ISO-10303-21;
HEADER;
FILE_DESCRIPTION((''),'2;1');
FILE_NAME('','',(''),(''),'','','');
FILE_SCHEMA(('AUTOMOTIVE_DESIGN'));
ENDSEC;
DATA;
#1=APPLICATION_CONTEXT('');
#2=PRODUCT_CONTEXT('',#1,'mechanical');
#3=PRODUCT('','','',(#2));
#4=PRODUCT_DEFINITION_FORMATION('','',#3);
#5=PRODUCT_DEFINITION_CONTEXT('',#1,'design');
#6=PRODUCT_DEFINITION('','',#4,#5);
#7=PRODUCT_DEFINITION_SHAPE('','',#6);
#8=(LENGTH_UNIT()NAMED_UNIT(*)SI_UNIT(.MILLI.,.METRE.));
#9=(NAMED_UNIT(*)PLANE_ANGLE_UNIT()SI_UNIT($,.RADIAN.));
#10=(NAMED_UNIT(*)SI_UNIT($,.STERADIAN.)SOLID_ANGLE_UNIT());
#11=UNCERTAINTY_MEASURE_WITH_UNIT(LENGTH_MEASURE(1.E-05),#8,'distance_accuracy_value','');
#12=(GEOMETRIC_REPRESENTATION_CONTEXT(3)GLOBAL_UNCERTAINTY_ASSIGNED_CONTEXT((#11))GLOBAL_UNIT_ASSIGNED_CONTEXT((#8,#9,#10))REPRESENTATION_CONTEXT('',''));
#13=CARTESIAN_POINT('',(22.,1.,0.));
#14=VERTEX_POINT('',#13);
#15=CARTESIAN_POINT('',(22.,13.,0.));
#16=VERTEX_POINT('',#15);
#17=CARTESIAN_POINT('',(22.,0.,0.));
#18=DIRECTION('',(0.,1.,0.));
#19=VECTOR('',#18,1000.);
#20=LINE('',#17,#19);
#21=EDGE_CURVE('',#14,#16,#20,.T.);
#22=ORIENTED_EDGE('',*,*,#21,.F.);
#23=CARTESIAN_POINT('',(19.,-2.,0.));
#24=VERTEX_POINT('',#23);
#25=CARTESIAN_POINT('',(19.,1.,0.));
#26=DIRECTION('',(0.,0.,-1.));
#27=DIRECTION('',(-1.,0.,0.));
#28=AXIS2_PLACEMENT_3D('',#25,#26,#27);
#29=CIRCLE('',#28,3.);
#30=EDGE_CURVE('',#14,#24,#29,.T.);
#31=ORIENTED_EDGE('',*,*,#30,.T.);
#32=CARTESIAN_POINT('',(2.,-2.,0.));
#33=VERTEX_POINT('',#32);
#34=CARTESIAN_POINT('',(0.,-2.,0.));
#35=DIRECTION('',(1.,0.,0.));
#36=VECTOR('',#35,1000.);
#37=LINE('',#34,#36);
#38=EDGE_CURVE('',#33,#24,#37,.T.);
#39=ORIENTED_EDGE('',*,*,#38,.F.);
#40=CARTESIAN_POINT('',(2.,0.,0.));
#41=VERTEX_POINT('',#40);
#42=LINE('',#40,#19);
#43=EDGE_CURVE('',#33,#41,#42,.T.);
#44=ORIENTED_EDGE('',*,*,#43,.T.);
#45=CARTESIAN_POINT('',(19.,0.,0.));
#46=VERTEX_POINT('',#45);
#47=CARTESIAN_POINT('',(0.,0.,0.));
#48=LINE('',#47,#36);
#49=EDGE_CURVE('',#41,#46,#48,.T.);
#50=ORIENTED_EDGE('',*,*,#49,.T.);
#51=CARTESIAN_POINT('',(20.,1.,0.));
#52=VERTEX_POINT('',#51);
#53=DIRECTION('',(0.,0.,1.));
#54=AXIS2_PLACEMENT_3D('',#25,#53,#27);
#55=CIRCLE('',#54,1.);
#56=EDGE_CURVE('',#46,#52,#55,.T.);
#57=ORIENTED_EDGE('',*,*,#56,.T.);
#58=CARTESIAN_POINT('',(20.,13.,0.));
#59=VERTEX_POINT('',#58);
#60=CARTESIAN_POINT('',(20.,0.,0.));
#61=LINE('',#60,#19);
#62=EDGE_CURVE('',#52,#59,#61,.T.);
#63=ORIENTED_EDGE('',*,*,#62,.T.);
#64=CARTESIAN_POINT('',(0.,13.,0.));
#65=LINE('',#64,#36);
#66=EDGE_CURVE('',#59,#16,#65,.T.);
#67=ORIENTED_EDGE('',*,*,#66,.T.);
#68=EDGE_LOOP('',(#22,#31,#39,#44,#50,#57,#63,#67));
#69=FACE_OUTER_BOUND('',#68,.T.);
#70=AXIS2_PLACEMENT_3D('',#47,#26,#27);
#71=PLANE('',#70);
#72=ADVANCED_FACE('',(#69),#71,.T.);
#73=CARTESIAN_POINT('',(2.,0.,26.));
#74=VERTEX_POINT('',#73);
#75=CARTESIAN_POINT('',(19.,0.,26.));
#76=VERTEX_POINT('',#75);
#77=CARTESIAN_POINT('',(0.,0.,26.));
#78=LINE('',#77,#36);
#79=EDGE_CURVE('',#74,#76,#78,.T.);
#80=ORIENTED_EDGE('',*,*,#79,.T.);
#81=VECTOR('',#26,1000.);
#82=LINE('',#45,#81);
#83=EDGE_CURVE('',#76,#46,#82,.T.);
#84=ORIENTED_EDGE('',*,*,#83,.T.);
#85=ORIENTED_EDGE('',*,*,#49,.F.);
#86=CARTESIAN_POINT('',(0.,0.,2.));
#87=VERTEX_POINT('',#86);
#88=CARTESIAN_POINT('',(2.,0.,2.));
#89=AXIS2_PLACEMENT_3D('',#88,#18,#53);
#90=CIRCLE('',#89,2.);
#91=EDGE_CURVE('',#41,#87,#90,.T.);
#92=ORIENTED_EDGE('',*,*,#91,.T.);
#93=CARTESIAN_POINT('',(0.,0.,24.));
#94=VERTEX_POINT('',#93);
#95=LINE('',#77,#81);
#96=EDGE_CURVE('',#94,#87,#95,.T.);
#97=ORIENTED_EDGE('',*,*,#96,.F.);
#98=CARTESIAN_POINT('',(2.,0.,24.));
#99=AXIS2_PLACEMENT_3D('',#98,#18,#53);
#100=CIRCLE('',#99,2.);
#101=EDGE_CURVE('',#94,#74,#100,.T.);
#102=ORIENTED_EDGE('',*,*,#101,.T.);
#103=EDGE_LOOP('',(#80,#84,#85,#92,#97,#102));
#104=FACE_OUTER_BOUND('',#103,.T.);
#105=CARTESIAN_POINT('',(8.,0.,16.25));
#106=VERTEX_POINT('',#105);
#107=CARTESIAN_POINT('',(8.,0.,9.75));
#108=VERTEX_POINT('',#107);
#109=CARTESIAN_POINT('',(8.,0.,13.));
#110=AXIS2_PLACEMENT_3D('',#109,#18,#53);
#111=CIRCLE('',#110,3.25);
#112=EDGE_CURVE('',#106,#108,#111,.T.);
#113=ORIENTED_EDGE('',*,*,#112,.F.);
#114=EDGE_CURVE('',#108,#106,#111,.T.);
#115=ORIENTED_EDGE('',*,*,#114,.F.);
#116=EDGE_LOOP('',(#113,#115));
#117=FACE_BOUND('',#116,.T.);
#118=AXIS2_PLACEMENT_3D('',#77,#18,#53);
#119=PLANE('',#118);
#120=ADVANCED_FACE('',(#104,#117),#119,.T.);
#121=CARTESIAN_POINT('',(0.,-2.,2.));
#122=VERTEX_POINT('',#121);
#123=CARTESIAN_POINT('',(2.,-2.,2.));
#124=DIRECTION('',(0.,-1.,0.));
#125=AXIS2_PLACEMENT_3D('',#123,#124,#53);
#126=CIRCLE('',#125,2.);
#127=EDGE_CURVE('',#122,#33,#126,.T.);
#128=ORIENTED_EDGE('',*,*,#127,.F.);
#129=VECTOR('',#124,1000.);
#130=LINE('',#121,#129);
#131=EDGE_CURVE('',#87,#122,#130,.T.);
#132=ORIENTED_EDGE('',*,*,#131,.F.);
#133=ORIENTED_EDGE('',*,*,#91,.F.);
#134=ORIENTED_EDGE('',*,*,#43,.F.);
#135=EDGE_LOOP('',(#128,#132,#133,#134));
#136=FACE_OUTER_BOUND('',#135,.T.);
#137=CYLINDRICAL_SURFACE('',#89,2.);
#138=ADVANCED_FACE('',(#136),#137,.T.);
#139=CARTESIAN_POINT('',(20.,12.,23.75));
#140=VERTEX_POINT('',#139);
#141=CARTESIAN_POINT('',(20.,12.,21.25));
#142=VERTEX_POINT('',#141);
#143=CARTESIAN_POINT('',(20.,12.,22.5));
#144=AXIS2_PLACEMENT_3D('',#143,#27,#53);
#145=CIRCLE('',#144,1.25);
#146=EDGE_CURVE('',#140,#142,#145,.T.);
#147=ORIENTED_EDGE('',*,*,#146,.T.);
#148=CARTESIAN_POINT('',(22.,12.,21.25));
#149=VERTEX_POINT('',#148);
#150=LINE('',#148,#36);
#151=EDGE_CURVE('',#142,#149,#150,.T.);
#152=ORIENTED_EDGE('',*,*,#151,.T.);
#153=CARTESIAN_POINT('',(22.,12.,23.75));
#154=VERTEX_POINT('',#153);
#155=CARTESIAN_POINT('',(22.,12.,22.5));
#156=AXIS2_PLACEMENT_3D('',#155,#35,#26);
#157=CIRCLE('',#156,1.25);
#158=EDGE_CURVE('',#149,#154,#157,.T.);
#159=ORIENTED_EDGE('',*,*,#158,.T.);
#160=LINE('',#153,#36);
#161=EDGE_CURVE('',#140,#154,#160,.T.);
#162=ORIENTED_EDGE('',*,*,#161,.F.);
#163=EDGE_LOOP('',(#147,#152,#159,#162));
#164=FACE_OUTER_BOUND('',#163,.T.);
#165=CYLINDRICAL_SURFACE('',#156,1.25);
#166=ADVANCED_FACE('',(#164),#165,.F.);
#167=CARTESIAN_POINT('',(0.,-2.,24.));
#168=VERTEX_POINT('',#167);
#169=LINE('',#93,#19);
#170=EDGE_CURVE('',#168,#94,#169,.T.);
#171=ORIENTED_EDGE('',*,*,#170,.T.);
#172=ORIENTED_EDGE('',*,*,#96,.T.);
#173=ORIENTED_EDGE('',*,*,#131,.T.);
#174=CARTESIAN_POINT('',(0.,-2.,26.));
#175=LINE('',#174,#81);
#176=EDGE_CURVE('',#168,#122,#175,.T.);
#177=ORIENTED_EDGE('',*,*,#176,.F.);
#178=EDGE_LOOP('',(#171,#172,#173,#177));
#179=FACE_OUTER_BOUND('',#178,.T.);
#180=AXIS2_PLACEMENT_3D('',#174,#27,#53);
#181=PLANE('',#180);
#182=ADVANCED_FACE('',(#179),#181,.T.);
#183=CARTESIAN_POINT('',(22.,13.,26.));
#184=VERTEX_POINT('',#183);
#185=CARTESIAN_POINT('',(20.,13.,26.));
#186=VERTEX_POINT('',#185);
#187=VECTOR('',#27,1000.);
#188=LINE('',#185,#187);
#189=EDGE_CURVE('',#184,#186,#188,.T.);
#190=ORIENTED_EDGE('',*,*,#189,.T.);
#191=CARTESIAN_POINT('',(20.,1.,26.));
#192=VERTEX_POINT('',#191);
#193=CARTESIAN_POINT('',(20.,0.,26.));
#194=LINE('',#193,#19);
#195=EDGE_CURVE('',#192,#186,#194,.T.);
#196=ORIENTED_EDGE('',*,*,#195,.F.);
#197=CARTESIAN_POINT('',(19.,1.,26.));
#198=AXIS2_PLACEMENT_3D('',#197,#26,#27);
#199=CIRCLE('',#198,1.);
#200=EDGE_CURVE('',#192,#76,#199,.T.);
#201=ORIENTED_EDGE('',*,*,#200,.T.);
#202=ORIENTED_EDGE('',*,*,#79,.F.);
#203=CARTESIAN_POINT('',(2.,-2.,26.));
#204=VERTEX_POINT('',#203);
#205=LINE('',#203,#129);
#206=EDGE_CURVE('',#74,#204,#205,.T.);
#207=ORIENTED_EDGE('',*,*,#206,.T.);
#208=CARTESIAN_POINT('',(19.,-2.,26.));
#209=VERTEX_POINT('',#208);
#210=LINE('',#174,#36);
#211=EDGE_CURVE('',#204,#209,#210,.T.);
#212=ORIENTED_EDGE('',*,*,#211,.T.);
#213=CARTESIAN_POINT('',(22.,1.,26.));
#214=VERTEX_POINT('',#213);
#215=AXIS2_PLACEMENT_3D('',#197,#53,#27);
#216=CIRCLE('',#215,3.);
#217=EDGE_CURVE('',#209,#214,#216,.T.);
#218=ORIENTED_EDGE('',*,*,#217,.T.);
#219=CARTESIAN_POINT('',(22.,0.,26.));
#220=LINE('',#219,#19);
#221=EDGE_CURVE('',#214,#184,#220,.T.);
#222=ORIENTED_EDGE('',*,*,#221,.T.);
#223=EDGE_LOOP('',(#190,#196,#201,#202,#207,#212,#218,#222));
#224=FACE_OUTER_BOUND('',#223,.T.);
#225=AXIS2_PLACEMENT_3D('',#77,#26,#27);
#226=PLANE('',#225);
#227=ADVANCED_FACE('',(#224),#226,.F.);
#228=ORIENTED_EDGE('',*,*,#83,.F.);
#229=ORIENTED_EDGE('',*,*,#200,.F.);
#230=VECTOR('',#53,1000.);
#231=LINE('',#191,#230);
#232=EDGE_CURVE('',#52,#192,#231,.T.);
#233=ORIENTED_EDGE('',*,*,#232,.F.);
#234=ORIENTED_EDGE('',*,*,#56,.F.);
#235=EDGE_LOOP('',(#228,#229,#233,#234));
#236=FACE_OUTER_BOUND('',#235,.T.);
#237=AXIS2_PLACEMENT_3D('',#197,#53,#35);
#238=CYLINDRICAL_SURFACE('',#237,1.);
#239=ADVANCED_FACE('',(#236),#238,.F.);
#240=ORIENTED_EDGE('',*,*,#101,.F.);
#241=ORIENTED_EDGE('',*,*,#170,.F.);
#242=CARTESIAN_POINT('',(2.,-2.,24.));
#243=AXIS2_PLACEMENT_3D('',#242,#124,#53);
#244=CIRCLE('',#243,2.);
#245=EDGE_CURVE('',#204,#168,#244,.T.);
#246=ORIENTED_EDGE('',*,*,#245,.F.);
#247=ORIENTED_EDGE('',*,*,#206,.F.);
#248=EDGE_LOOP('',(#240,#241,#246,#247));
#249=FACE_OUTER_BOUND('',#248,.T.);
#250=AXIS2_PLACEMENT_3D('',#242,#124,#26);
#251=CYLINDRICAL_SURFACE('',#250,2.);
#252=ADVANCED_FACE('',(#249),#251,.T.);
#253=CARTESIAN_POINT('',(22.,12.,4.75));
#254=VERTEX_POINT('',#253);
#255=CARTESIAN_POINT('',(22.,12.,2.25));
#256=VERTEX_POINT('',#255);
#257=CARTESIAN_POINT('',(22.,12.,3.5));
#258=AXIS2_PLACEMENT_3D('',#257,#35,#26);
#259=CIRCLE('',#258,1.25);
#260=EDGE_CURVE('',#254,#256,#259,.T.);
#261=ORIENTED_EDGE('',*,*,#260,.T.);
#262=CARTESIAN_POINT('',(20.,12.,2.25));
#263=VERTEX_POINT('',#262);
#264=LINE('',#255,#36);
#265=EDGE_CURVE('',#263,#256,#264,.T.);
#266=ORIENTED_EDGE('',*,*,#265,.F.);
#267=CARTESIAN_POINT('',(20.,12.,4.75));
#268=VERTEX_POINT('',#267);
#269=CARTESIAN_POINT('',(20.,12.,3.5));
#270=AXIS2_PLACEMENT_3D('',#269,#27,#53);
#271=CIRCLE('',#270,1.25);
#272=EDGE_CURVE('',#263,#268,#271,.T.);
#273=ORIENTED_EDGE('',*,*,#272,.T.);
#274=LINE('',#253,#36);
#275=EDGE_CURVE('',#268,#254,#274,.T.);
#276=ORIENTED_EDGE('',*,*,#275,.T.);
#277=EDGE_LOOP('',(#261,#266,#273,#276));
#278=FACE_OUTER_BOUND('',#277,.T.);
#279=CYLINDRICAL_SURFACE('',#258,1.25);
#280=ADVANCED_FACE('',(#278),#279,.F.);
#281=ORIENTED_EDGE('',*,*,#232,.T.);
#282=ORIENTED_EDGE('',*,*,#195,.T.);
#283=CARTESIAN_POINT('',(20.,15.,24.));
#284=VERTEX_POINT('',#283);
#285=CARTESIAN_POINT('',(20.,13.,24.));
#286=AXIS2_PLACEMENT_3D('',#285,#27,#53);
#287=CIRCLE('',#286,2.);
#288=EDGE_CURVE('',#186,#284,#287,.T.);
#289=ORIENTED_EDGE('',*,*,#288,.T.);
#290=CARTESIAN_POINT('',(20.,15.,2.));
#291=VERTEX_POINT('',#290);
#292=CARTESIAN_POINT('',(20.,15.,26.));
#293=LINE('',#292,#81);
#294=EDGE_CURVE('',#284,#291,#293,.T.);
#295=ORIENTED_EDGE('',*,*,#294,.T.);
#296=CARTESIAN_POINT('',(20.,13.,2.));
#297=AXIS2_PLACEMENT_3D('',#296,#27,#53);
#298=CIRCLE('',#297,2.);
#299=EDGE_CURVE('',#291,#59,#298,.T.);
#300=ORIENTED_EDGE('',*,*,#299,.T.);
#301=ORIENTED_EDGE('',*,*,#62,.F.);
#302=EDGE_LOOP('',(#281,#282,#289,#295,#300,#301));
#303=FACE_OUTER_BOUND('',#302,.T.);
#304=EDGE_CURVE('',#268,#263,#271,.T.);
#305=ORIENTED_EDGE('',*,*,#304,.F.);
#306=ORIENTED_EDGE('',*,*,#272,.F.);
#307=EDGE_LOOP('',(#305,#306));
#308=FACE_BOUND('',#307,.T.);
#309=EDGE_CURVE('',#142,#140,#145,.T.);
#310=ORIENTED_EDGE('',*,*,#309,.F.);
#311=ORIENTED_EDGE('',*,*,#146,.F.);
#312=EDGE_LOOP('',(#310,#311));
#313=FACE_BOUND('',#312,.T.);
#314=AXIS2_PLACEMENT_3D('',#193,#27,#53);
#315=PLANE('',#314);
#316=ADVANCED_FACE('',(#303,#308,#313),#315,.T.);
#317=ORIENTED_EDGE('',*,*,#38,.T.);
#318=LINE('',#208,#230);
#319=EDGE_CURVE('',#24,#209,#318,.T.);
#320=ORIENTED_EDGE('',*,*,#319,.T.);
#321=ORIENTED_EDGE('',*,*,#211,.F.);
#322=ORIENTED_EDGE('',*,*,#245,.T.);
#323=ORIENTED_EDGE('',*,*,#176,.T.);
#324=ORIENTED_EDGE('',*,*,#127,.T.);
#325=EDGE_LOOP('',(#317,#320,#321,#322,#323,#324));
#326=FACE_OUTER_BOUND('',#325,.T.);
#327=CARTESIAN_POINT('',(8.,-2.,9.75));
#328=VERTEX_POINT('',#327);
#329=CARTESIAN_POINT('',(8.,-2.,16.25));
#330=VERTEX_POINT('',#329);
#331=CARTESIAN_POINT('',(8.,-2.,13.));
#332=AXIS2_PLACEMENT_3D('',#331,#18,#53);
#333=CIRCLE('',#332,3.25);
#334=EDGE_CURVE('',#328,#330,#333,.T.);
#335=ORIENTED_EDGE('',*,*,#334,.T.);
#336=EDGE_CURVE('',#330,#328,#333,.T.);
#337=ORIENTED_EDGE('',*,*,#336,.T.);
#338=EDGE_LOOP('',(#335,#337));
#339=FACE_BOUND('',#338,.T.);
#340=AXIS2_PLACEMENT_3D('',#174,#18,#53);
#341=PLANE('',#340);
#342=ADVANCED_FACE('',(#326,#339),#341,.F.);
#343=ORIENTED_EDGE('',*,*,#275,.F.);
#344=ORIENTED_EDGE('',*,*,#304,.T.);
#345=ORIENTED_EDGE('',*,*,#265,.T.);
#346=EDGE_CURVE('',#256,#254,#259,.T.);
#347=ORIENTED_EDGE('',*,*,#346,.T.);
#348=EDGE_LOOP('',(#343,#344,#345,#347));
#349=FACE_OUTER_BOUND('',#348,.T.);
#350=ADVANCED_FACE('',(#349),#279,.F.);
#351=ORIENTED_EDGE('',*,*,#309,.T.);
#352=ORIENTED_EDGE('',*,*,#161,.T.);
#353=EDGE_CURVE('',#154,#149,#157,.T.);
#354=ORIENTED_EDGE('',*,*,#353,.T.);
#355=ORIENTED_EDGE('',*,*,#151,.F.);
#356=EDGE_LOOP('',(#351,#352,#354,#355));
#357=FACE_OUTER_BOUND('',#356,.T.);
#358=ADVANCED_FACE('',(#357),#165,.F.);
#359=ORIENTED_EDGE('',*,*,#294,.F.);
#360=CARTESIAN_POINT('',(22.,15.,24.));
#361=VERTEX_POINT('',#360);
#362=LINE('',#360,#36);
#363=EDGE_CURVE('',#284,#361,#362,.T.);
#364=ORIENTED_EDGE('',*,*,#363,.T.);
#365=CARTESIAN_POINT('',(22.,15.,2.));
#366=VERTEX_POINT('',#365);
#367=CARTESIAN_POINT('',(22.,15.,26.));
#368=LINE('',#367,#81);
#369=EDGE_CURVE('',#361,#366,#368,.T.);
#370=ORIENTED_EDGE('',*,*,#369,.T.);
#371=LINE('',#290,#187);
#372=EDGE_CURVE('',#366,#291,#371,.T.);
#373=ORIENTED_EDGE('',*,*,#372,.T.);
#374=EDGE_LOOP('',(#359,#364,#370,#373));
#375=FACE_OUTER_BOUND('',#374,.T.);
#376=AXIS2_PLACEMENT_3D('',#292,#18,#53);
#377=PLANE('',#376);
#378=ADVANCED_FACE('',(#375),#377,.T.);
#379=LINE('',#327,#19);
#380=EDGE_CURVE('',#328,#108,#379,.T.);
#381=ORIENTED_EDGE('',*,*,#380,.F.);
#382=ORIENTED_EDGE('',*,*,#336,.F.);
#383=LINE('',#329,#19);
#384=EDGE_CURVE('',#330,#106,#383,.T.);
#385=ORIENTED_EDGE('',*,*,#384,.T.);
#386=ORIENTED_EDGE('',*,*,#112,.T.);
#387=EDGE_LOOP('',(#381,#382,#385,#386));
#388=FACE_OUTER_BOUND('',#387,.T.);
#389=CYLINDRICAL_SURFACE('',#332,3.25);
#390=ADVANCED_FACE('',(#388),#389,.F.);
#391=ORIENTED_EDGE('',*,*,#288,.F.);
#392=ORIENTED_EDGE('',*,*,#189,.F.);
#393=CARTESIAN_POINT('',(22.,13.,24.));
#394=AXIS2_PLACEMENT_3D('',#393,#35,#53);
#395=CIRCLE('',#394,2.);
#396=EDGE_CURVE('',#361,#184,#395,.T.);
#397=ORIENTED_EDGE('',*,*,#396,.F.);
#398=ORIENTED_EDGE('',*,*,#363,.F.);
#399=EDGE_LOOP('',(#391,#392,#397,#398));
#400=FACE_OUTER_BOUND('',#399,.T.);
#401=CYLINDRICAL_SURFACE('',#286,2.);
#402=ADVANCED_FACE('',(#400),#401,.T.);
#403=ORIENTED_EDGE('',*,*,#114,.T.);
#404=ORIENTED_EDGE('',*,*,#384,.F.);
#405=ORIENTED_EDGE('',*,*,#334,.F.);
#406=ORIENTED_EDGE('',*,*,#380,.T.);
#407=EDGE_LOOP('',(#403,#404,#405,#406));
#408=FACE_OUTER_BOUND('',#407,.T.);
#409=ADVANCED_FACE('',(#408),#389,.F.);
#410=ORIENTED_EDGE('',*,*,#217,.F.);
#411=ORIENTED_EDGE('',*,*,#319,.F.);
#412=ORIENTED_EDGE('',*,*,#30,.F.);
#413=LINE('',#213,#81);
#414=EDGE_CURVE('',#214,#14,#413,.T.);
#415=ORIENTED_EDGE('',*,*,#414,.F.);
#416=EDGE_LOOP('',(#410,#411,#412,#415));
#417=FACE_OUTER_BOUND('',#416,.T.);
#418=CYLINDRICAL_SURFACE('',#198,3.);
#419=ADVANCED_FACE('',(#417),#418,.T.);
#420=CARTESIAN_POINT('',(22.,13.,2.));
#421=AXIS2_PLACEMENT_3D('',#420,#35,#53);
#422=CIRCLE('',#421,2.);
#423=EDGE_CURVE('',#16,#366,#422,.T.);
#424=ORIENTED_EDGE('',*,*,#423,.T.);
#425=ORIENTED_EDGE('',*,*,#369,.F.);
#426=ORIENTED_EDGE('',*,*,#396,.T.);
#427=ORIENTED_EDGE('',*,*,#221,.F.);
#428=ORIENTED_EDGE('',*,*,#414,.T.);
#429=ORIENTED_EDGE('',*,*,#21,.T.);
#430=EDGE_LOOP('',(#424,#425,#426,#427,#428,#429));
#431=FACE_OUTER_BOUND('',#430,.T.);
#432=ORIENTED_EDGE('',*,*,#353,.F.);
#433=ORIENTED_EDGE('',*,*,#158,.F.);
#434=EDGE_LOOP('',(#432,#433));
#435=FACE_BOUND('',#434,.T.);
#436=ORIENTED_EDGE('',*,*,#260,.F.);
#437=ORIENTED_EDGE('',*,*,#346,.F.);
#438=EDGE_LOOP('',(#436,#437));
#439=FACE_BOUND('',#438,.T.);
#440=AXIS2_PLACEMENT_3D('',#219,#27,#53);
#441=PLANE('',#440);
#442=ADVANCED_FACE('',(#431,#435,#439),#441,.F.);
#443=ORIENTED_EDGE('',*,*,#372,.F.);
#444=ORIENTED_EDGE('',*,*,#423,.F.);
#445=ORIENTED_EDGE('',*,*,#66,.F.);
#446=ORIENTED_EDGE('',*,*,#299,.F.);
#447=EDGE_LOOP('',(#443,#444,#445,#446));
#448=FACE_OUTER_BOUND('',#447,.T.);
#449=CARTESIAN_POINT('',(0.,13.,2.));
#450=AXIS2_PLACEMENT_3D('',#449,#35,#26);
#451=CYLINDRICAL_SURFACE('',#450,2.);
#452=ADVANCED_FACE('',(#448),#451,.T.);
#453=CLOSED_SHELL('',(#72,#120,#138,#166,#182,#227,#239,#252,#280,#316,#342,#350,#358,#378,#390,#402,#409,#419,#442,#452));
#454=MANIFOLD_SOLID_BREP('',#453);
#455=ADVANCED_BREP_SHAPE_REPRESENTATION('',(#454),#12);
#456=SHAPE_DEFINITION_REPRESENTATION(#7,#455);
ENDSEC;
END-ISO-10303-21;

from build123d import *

# Parameters (mm, degrees)
EXTRUDE_1_DEPTH     = 26
FILLET_1_R          = 1
FILLET_2_R          = 3
FILLET_3_R          = 2
SKETCH_2_R          = 3.25
CUT_EXTRUDE_1_DEPTH = 38.215588132
HOLE_WIZARD_M3_1_D  = 2.5


with BuildPart() as part:
    # 草图1 → 拉伸-薄壁1 (new body)
    with BuildSketch(Plane.XY):
        Polygon((0, 0), (20, 0), (20, 15), (22, 15), (22, -2), (0, -2), align=None)
    extrude(amount=EXTRUDE_1_DEPTH)

    # 圆角1
    fillet_1_edges = [part.edges().sort_by_distance(p)[0] for p in [
        (20, 0, 13),
    ]]
    fillet(fillet_1_edges, radius=FILLET_1_R)

    # 圆角2
    fillet_2_edges = [part.edges().sort_by_distance(p)[0] for p in [
        (22, -2, 13),
    ]]
    fillet(fillet_2_edges, radius=FILLET_2_R)

    # 圆角3
    fillet_3_edges = [part.edges().sort_by_distance(p)[0] for p in [
        (0, -1, 26),
        (0, -1, 0),
        (21, 15, 0),
        (21, 15, 26),
    ]]
    fillet(fillet_3_edges, radius=FILLET_3_R)

    # 草图2 → 切除-拉伸1 (cut, through all)
    with BuildSketch(Plane(origin=(0, 0, 0), x_dir=(1, 0, 0), z_dir=(0, 1, 0))):
        with Locations(Location((8, -13, 0), (0, 0, 270))):
            Circle(SKETCH_2_R)
    extrude(amount=-CUT_EXTRUDE_1_DEPTH, mode=Mode.SUBTRACT)

    # M3 螺纹孔1 (through all)
    with Locations(Plane(origin=(22, 0, 0), x_dir=(0, 0, -1), z_dir=(1, 0, 0))):
        with Locations((-22.5, 12), (-3.5, 12)):
            Hole(HOLE_WIZARD_M3_1_D / 2)


solid = part.part
